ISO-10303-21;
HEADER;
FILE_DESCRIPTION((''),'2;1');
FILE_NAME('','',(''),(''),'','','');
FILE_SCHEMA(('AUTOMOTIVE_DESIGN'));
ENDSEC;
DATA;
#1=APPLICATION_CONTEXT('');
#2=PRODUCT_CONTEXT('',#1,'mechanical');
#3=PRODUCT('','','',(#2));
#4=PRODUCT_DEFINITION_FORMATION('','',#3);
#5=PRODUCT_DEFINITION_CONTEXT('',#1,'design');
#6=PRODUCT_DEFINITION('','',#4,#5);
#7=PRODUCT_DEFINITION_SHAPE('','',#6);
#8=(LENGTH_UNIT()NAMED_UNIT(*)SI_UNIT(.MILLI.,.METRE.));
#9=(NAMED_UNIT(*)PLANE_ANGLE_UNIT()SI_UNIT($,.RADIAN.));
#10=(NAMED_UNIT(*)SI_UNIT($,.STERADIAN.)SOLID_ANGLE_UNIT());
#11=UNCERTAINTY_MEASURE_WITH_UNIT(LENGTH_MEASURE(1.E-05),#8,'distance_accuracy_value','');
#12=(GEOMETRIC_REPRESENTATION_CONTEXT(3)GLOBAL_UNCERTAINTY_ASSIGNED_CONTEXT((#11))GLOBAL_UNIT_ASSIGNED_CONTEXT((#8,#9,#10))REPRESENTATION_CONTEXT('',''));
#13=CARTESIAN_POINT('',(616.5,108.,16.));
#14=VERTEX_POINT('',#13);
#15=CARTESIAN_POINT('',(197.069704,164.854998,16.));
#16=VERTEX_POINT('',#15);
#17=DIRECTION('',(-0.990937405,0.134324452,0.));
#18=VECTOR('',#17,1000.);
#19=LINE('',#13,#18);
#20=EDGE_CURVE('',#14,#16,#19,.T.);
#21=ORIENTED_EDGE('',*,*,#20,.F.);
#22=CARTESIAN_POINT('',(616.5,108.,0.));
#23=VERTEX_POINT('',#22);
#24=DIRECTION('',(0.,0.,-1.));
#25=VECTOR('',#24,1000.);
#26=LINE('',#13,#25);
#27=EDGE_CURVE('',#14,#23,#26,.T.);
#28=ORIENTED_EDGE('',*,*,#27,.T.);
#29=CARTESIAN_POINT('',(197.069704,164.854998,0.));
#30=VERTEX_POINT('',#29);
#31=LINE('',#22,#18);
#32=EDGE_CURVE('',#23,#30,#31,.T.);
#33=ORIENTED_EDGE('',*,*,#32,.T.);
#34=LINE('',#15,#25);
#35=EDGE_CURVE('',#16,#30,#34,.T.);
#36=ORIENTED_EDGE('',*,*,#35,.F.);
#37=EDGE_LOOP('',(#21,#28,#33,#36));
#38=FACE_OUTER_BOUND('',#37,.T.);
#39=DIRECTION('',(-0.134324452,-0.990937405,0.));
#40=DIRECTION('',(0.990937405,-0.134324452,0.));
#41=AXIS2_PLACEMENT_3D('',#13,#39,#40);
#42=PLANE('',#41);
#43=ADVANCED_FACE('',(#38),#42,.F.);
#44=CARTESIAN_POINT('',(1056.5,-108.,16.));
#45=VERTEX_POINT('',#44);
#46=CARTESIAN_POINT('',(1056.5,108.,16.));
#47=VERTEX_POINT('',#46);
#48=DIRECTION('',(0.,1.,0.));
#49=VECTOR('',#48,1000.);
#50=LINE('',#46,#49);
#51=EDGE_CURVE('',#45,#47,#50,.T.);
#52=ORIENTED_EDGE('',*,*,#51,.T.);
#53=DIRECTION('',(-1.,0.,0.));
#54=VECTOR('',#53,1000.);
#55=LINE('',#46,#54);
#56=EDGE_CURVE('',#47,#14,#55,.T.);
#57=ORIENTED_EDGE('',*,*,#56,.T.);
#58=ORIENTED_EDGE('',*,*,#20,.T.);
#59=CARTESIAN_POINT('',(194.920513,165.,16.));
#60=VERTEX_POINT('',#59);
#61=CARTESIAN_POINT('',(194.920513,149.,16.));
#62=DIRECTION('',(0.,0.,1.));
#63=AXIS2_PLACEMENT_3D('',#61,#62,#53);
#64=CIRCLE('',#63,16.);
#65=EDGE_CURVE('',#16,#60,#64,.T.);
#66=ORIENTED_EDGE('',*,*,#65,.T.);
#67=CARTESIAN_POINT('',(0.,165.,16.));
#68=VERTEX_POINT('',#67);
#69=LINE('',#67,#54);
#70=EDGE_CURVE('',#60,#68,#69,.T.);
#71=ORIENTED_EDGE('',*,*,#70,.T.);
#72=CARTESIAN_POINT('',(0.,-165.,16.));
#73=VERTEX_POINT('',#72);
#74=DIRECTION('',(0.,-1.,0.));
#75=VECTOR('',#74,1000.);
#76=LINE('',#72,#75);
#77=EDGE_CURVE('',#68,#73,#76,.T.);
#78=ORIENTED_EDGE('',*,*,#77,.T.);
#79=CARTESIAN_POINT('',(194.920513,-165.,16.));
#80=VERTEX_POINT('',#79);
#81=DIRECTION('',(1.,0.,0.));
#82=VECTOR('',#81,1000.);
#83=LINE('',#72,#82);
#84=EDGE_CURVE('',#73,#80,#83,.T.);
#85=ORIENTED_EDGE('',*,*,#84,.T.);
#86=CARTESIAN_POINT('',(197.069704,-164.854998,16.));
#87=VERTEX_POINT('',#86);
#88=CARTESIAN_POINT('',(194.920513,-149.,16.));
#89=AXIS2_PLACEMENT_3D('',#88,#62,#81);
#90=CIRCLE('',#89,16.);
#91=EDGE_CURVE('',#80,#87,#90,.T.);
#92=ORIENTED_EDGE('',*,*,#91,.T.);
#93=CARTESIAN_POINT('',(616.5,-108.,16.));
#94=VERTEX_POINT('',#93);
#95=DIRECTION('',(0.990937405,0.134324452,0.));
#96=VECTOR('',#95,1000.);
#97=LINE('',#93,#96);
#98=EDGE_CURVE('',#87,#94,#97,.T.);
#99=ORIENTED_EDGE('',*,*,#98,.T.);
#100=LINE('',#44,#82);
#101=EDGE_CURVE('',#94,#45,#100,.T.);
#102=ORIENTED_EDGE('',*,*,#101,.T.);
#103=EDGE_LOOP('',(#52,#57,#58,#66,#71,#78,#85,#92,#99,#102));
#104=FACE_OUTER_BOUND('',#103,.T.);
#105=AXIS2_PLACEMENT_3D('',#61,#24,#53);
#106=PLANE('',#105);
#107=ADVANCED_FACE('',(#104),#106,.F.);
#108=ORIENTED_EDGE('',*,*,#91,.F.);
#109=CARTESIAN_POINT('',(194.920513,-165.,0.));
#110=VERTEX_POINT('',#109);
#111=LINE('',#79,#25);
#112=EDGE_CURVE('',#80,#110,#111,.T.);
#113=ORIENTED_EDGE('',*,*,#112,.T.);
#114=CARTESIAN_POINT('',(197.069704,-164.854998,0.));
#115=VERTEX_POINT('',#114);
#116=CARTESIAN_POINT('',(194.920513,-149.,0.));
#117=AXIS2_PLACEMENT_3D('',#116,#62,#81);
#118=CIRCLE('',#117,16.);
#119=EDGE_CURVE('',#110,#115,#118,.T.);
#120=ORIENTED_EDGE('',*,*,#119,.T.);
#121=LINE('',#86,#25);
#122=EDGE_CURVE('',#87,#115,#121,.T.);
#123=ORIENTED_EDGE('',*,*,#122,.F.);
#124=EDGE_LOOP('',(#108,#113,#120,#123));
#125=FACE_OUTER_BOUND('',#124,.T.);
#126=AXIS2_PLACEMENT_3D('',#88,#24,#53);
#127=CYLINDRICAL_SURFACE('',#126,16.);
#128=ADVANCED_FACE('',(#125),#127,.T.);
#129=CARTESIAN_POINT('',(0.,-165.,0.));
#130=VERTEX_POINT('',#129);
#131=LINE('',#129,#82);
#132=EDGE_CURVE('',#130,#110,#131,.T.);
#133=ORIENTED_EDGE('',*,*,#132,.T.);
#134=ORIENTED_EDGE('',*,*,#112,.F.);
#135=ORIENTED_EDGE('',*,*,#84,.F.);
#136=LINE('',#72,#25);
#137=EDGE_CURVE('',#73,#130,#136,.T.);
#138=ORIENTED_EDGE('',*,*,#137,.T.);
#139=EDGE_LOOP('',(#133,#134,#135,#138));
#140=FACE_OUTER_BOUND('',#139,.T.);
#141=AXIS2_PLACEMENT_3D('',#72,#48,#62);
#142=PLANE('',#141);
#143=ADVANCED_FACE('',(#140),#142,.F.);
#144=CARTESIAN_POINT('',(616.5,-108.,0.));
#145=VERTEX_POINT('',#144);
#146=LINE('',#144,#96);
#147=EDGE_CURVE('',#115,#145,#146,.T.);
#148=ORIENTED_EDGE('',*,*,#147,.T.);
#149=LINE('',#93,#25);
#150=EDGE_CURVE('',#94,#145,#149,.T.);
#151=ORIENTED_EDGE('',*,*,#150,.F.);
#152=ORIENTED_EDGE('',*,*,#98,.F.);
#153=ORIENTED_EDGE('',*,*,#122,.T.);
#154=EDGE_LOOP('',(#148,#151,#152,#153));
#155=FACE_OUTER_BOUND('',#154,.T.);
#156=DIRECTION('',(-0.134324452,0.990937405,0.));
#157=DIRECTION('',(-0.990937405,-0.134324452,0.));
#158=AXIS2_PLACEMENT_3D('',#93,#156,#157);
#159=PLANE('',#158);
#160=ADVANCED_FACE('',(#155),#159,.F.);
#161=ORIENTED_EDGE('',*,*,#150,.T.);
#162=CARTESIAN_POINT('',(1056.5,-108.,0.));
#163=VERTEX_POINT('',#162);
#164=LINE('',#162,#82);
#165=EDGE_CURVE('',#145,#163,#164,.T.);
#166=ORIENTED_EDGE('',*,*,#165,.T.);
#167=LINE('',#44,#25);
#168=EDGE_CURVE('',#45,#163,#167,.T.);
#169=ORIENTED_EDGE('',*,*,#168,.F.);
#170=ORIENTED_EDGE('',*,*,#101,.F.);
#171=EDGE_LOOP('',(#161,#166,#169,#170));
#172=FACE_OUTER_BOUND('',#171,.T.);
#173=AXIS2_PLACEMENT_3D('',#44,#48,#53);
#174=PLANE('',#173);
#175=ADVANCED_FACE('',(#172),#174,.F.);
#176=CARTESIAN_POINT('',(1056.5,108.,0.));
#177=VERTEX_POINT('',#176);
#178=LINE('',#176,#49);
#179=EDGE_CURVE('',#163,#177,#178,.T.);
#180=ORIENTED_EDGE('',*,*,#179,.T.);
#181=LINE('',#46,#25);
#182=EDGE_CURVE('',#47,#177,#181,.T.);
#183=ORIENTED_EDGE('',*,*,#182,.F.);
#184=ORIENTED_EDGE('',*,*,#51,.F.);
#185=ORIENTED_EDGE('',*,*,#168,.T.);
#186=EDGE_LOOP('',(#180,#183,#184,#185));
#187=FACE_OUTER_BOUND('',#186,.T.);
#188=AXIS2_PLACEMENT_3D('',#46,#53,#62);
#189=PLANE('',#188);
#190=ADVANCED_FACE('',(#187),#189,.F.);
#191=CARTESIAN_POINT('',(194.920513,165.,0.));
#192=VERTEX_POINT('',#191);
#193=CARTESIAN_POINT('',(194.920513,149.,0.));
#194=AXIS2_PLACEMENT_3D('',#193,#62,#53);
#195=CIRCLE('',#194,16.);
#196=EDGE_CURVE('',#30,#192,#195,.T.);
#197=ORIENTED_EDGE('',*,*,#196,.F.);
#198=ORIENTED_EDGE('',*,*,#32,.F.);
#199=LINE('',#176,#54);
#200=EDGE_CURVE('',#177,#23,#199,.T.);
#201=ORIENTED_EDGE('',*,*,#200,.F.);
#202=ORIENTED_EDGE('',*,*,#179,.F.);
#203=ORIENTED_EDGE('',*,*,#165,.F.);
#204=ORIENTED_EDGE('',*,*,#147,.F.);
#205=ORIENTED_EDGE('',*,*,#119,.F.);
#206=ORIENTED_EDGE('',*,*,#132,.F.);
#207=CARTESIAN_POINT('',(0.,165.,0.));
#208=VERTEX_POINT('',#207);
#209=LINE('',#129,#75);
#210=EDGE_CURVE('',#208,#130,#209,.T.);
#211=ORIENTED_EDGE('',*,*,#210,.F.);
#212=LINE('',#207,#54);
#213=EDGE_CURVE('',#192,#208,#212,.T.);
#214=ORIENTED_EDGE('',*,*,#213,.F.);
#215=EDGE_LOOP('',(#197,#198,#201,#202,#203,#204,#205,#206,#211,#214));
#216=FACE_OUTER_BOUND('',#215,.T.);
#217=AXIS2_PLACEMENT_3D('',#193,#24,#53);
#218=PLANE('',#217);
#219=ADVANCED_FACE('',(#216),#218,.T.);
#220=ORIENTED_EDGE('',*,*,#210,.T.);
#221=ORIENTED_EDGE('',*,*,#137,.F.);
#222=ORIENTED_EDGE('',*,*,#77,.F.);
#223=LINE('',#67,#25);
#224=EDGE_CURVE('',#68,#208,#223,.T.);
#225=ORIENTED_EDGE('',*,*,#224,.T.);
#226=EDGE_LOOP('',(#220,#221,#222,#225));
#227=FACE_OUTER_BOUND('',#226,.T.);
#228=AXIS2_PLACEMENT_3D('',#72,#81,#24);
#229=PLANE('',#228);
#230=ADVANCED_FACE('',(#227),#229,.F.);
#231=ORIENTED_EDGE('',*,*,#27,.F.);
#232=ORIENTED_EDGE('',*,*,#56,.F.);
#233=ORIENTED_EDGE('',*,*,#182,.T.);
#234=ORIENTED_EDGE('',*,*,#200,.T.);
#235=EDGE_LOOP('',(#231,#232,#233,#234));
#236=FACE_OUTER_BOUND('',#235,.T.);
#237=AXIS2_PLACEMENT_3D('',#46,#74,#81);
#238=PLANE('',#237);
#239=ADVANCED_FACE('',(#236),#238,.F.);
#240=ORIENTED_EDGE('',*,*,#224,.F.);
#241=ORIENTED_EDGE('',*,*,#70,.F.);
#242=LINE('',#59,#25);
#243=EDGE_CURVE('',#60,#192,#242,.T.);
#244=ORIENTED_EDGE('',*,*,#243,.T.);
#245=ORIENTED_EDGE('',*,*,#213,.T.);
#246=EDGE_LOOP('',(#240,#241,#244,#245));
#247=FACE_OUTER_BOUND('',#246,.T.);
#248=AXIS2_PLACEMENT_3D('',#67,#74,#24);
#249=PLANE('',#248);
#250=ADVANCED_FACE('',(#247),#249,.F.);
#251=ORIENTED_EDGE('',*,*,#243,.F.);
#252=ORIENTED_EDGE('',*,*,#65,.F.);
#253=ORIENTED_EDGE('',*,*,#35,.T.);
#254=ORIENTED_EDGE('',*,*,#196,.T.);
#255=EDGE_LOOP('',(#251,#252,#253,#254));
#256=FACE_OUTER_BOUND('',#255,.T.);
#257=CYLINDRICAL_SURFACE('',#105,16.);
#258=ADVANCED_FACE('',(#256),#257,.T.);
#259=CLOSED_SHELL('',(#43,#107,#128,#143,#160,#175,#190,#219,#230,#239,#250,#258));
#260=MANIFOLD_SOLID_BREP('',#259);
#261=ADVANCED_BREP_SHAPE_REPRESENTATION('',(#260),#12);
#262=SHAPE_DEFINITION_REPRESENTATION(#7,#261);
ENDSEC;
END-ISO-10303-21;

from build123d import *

# Parameters (mm, degrees)
BOSS_EXTRUDE1_DEPTH = 16


with BuildPart() as part:
    # Sketch1 → Boss-Extrude1 (new body)
    with BuildSketch(Plane.XY):
        with BuildLine():
            Line((0, 165), (194.920512906, 165))
            ThreePointArc((194.920512906, 165), (195.997551485, 164.963708463), (197.06970414, 164.854998488))
            Line((197.06970414, 164.854998488), (616.5, 108))
            Line((616.5, 108), (1056.5, 108))
            Line((1056.5, 108), (1056.5, -108))
            Line((1056.5, -108), (616.5, -108))
            Line((616.5, -108), (197.06970414, -164.854998488))
            ThreePointArc((197.06970414, -164.854998488), (195.997551485, -164.963708463), (194.920512906, -165))
            Line((194.920512906, -165), (0, -165))
            Line((0, -165), (0, 165))
        make_face()
    extrude(amount=BOSS_EXTRUDE1_DEPTH)


solid = part.part
